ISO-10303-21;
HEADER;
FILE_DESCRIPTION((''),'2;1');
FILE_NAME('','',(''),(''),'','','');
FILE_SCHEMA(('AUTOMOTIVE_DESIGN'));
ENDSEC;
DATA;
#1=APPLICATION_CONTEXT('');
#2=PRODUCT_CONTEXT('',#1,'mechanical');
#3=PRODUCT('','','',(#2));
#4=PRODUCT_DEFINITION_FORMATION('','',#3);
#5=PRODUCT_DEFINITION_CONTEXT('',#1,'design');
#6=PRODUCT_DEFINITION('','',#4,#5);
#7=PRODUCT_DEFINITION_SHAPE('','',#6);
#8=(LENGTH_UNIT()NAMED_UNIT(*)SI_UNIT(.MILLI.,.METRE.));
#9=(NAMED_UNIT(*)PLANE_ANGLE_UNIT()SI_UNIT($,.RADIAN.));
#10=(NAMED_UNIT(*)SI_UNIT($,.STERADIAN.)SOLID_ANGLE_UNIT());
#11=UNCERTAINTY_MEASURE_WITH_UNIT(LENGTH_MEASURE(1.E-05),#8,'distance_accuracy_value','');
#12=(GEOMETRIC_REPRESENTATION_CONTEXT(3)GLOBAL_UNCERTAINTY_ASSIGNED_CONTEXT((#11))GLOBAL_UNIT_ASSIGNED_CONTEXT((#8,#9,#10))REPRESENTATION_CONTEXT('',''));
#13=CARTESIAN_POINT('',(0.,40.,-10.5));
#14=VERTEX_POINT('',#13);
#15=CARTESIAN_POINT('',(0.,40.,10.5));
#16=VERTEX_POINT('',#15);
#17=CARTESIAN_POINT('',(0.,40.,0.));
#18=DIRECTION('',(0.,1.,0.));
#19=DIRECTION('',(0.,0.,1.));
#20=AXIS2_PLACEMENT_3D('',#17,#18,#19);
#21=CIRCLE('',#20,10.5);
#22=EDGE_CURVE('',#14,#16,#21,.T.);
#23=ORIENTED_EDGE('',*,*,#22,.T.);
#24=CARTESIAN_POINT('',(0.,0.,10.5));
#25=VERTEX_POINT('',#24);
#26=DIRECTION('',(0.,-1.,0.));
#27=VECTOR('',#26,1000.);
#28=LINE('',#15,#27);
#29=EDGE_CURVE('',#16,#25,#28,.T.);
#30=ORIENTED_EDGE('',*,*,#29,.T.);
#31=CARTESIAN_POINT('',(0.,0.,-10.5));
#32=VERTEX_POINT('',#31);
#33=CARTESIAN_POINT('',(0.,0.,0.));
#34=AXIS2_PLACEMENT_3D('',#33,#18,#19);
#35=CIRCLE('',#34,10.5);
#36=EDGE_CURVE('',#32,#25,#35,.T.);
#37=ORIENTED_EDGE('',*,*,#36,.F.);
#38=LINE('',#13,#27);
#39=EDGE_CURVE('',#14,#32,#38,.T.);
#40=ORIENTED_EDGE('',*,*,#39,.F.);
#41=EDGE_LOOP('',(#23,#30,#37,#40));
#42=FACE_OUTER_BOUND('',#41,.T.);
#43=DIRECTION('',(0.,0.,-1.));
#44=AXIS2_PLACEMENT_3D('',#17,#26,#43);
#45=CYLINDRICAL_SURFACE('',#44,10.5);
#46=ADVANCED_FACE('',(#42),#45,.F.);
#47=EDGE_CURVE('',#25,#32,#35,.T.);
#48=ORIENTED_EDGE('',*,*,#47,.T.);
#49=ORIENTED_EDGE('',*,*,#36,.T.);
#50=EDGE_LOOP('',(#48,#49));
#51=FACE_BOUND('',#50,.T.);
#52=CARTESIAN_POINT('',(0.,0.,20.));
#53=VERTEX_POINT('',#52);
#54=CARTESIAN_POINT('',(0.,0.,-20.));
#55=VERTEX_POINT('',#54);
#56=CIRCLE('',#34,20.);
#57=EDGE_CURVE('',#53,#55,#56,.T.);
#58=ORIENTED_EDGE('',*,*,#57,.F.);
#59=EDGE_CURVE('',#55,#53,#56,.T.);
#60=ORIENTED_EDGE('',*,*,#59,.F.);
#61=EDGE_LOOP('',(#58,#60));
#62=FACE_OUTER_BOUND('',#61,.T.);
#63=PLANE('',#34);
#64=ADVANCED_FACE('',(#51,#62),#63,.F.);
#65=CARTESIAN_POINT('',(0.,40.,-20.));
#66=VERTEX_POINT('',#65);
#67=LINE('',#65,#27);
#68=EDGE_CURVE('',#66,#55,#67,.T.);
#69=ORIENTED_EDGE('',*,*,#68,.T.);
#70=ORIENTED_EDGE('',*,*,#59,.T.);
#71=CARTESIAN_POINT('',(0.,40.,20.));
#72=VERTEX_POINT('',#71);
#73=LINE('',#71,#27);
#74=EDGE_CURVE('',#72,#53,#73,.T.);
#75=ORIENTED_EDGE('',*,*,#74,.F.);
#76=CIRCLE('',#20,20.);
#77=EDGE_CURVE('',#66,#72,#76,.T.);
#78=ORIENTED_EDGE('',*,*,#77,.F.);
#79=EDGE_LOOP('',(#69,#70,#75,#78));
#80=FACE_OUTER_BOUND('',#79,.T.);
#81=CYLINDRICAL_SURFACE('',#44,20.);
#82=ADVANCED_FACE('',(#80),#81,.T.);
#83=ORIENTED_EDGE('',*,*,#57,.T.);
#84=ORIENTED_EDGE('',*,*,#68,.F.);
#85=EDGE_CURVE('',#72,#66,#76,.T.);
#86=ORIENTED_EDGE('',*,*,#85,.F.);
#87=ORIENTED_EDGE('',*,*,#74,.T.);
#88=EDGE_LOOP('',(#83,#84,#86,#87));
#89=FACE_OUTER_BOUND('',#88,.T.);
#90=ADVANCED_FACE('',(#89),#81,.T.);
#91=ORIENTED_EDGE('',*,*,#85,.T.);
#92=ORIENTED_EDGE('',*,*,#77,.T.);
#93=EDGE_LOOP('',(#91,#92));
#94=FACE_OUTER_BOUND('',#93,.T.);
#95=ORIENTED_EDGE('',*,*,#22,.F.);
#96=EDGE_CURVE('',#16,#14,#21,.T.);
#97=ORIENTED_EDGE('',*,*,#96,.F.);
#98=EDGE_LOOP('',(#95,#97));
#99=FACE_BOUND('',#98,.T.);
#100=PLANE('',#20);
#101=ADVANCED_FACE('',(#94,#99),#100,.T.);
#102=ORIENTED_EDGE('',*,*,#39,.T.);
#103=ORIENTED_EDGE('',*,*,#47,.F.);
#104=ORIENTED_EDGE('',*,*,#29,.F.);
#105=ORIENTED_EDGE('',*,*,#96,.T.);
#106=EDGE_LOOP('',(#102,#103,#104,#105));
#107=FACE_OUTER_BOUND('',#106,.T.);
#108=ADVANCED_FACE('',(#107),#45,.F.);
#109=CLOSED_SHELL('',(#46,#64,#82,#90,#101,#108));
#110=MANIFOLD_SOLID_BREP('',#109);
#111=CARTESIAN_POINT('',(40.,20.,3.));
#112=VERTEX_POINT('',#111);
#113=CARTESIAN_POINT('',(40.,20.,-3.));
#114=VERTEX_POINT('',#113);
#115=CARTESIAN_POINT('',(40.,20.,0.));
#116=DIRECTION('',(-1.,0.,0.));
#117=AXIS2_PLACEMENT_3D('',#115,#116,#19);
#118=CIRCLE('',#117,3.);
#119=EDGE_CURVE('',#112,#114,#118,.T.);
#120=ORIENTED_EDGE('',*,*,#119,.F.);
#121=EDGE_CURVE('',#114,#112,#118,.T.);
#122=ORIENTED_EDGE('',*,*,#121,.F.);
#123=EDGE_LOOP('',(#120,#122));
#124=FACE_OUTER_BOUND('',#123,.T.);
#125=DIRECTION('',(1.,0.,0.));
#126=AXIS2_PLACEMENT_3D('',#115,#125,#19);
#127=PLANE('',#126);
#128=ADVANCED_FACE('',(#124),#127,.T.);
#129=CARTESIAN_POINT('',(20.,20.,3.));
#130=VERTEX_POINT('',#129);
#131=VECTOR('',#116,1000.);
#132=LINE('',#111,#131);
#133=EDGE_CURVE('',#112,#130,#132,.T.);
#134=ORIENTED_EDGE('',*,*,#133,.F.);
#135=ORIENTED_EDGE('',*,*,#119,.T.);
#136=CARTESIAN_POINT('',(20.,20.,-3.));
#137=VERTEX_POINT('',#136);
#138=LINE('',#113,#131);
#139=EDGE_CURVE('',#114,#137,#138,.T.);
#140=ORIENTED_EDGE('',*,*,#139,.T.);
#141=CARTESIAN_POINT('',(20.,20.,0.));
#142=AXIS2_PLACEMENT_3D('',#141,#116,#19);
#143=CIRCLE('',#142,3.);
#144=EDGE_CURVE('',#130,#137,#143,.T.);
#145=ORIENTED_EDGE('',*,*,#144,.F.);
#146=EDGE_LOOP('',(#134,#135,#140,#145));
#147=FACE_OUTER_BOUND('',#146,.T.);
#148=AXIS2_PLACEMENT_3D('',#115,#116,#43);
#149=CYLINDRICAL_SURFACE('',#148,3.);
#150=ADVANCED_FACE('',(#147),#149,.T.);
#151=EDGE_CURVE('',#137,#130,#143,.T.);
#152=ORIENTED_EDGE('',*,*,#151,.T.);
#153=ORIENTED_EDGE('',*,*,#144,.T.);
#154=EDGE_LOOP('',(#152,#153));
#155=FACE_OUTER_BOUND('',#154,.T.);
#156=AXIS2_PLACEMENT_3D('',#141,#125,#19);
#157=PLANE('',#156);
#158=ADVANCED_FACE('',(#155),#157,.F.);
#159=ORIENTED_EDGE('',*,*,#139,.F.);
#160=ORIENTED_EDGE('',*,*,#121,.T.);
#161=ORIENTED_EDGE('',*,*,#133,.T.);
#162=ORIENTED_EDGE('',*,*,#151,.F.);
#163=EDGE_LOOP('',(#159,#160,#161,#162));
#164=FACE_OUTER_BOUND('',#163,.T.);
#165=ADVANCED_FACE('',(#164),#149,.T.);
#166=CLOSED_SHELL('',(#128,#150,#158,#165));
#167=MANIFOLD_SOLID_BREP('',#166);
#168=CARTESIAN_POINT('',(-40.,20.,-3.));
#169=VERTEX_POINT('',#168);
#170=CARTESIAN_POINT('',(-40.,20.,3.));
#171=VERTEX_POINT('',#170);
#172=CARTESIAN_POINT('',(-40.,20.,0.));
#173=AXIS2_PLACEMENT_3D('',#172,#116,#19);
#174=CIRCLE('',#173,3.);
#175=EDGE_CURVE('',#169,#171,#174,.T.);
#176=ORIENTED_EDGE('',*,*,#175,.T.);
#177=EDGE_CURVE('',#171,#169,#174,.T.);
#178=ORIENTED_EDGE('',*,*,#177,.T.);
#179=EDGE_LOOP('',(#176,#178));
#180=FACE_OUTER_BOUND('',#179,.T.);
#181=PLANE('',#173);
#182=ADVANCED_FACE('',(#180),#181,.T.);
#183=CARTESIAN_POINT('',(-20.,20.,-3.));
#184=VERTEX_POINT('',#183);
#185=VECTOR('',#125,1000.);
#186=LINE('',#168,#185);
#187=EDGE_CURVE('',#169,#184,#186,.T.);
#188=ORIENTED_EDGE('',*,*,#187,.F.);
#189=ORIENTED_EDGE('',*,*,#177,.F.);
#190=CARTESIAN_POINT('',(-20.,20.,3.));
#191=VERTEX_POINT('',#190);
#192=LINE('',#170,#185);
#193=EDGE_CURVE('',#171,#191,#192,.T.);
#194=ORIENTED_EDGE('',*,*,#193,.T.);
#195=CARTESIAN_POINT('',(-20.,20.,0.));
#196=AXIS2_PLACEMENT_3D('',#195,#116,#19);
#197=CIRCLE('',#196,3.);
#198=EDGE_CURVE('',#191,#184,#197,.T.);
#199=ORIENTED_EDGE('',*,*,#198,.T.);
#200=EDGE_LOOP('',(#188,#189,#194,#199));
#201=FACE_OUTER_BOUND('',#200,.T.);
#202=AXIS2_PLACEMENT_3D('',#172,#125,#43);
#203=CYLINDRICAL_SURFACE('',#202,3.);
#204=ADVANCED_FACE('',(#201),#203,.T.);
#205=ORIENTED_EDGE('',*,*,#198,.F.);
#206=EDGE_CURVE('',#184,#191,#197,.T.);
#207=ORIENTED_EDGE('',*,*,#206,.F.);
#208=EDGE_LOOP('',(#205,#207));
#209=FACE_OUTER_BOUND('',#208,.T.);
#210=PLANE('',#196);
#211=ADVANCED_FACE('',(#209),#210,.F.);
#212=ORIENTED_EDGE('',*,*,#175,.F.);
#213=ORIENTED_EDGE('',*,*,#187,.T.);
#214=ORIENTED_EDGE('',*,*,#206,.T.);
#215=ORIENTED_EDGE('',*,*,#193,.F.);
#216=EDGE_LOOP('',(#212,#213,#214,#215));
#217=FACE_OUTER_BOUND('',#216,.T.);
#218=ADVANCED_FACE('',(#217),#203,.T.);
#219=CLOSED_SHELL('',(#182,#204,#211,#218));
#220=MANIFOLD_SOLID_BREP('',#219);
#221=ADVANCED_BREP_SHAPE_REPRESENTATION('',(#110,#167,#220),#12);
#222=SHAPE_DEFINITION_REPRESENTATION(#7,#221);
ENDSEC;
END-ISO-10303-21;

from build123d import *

# Parameters (mm, degrees)
SKETCH_2_R      = 20
SKETCH_2_R_2    = 10.5
EXTRUDE_1_DEPTH = 40
SKETCH_3_R      = 3
EXTRUDE_2_DEPTH = 20


with BuildPart() as part:
    # 草图2 → 凸台-拉伸1 (new body)
    with BuildSketch(Plane(origin=(0, 0, 0), x_dir=(1, 0, 0), z_dir=(0, 1, 0))):
        with Locations(Location((0, 0, 0), (0, 0, 270))):
            Circle(SKETCH_2_R)
        with Locations(Location((0, 0, 0), (0, 0, 270))):
            Circle(SKETCH_2_R_2, mode=Mode.SUBTRACT)
    extrude(amount=EXTRUDE_1_DEPTH)


with BuildPart() as body_2:
    # 草图3 → 凸台-拉伸2 (new body)
    with BuildSketch(Plane.ZY.offset(20)):
        with Locations((0, 20)):
            Circle(SKETCH_3_R)
    extrude(amount=EXTRUDE_2_DEPTH)


with BuildPart() as body_3:
    # 镜向3: mirrored copy
    add(body_2.part.mirror(Plane(origin=(0, 0, 0), x_dir=(0, 0, 1), z_dir=(1, 0, 0))))


solid = Compound([part.part, body_2.part, body_3.part])
